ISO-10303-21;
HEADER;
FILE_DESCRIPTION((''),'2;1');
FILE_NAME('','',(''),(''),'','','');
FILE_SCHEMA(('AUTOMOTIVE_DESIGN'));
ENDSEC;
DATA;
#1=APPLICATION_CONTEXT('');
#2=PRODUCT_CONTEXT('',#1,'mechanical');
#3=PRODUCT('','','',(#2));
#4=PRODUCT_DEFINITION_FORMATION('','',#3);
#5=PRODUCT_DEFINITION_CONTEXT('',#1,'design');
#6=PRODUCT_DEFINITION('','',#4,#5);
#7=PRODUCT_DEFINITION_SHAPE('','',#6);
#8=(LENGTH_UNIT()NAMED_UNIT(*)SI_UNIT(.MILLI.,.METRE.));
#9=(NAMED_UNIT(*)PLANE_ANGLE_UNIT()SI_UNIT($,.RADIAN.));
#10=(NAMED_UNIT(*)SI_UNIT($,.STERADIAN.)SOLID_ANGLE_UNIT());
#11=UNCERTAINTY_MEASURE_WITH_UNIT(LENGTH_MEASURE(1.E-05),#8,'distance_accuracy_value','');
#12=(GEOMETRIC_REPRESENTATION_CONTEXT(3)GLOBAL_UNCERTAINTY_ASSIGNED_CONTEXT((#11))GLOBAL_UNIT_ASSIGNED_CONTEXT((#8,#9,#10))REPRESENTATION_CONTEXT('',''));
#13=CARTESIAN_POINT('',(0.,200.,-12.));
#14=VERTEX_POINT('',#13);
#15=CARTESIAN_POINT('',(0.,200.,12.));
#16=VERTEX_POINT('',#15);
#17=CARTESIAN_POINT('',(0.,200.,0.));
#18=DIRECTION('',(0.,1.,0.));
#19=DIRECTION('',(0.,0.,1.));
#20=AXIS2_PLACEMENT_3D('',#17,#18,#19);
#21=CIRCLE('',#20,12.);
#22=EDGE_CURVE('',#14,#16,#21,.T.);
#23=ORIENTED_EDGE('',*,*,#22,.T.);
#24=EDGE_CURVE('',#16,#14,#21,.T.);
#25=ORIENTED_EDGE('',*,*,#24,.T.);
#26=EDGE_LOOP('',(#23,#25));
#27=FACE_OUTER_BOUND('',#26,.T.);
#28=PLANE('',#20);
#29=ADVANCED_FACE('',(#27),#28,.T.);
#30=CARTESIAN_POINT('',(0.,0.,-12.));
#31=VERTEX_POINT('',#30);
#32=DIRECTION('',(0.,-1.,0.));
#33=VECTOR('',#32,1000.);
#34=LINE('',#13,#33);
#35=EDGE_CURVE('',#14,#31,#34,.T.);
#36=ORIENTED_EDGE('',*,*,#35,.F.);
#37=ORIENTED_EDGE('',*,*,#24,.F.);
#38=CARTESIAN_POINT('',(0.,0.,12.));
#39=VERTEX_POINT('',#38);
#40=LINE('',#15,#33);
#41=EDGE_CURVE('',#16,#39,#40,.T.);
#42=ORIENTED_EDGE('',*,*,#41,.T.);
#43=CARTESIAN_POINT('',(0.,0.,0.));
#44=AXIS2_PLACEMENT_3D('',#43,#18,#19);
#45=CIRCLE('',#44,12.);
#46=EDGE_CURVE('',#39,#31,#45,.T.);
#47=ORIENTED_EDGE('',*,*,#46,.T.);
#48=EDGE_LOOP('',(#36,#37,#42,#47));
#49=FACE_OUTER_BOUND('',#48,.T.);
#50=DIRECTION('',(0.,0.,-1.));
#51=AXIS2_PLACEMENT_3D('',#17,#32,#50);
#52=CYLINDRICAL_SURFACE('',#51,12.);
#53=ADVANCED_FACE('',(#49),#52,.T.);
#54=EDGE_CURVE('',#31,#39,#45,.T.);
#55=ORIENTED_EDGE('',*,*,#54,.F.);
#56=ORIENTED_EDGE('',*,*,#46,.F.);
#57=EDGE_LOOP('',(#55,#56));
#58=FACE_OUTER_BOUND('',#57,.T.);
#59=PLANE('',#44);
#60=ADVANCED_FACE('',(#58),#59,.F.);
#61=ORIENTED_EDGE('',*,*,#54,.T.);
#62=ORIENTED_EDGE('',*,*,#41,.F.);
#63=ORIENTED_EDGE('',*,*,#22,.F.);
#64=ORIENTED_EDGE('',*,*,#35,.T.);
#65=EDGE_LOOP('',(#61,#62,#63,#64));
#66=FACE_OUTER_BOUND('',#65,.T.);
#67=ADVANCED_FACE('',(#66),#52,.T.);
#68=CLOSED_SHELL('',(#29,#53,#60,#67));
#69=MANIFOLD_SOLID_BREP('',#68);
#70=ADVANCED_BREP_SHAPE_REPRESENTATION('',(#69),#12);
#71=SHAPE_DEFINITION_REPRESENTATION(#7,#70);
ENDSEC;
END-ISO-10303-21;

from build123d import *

# Parameters (mm, degrees)
SHAFT_PROFILE_24_R   = 12
SHAFT_24_X_200_DEPTH = 200


with BuildPart() as part:
    # Shaft Profile Ø24 → Shaft Ø24 x 200 (new body)
    with BuildSketch(Plane(origin=(0, 0, 0), x_dir=(1, 0, 0), z_dir=(0, 1, 0))):
        with Locations(Location((0, 0, 0), (0, 0, 270))):
            Circle(SHAFT_PROFILE_24_R)
    extrude(amount=SHAFT_24_X_200_DEPTH)


solid = part.part
